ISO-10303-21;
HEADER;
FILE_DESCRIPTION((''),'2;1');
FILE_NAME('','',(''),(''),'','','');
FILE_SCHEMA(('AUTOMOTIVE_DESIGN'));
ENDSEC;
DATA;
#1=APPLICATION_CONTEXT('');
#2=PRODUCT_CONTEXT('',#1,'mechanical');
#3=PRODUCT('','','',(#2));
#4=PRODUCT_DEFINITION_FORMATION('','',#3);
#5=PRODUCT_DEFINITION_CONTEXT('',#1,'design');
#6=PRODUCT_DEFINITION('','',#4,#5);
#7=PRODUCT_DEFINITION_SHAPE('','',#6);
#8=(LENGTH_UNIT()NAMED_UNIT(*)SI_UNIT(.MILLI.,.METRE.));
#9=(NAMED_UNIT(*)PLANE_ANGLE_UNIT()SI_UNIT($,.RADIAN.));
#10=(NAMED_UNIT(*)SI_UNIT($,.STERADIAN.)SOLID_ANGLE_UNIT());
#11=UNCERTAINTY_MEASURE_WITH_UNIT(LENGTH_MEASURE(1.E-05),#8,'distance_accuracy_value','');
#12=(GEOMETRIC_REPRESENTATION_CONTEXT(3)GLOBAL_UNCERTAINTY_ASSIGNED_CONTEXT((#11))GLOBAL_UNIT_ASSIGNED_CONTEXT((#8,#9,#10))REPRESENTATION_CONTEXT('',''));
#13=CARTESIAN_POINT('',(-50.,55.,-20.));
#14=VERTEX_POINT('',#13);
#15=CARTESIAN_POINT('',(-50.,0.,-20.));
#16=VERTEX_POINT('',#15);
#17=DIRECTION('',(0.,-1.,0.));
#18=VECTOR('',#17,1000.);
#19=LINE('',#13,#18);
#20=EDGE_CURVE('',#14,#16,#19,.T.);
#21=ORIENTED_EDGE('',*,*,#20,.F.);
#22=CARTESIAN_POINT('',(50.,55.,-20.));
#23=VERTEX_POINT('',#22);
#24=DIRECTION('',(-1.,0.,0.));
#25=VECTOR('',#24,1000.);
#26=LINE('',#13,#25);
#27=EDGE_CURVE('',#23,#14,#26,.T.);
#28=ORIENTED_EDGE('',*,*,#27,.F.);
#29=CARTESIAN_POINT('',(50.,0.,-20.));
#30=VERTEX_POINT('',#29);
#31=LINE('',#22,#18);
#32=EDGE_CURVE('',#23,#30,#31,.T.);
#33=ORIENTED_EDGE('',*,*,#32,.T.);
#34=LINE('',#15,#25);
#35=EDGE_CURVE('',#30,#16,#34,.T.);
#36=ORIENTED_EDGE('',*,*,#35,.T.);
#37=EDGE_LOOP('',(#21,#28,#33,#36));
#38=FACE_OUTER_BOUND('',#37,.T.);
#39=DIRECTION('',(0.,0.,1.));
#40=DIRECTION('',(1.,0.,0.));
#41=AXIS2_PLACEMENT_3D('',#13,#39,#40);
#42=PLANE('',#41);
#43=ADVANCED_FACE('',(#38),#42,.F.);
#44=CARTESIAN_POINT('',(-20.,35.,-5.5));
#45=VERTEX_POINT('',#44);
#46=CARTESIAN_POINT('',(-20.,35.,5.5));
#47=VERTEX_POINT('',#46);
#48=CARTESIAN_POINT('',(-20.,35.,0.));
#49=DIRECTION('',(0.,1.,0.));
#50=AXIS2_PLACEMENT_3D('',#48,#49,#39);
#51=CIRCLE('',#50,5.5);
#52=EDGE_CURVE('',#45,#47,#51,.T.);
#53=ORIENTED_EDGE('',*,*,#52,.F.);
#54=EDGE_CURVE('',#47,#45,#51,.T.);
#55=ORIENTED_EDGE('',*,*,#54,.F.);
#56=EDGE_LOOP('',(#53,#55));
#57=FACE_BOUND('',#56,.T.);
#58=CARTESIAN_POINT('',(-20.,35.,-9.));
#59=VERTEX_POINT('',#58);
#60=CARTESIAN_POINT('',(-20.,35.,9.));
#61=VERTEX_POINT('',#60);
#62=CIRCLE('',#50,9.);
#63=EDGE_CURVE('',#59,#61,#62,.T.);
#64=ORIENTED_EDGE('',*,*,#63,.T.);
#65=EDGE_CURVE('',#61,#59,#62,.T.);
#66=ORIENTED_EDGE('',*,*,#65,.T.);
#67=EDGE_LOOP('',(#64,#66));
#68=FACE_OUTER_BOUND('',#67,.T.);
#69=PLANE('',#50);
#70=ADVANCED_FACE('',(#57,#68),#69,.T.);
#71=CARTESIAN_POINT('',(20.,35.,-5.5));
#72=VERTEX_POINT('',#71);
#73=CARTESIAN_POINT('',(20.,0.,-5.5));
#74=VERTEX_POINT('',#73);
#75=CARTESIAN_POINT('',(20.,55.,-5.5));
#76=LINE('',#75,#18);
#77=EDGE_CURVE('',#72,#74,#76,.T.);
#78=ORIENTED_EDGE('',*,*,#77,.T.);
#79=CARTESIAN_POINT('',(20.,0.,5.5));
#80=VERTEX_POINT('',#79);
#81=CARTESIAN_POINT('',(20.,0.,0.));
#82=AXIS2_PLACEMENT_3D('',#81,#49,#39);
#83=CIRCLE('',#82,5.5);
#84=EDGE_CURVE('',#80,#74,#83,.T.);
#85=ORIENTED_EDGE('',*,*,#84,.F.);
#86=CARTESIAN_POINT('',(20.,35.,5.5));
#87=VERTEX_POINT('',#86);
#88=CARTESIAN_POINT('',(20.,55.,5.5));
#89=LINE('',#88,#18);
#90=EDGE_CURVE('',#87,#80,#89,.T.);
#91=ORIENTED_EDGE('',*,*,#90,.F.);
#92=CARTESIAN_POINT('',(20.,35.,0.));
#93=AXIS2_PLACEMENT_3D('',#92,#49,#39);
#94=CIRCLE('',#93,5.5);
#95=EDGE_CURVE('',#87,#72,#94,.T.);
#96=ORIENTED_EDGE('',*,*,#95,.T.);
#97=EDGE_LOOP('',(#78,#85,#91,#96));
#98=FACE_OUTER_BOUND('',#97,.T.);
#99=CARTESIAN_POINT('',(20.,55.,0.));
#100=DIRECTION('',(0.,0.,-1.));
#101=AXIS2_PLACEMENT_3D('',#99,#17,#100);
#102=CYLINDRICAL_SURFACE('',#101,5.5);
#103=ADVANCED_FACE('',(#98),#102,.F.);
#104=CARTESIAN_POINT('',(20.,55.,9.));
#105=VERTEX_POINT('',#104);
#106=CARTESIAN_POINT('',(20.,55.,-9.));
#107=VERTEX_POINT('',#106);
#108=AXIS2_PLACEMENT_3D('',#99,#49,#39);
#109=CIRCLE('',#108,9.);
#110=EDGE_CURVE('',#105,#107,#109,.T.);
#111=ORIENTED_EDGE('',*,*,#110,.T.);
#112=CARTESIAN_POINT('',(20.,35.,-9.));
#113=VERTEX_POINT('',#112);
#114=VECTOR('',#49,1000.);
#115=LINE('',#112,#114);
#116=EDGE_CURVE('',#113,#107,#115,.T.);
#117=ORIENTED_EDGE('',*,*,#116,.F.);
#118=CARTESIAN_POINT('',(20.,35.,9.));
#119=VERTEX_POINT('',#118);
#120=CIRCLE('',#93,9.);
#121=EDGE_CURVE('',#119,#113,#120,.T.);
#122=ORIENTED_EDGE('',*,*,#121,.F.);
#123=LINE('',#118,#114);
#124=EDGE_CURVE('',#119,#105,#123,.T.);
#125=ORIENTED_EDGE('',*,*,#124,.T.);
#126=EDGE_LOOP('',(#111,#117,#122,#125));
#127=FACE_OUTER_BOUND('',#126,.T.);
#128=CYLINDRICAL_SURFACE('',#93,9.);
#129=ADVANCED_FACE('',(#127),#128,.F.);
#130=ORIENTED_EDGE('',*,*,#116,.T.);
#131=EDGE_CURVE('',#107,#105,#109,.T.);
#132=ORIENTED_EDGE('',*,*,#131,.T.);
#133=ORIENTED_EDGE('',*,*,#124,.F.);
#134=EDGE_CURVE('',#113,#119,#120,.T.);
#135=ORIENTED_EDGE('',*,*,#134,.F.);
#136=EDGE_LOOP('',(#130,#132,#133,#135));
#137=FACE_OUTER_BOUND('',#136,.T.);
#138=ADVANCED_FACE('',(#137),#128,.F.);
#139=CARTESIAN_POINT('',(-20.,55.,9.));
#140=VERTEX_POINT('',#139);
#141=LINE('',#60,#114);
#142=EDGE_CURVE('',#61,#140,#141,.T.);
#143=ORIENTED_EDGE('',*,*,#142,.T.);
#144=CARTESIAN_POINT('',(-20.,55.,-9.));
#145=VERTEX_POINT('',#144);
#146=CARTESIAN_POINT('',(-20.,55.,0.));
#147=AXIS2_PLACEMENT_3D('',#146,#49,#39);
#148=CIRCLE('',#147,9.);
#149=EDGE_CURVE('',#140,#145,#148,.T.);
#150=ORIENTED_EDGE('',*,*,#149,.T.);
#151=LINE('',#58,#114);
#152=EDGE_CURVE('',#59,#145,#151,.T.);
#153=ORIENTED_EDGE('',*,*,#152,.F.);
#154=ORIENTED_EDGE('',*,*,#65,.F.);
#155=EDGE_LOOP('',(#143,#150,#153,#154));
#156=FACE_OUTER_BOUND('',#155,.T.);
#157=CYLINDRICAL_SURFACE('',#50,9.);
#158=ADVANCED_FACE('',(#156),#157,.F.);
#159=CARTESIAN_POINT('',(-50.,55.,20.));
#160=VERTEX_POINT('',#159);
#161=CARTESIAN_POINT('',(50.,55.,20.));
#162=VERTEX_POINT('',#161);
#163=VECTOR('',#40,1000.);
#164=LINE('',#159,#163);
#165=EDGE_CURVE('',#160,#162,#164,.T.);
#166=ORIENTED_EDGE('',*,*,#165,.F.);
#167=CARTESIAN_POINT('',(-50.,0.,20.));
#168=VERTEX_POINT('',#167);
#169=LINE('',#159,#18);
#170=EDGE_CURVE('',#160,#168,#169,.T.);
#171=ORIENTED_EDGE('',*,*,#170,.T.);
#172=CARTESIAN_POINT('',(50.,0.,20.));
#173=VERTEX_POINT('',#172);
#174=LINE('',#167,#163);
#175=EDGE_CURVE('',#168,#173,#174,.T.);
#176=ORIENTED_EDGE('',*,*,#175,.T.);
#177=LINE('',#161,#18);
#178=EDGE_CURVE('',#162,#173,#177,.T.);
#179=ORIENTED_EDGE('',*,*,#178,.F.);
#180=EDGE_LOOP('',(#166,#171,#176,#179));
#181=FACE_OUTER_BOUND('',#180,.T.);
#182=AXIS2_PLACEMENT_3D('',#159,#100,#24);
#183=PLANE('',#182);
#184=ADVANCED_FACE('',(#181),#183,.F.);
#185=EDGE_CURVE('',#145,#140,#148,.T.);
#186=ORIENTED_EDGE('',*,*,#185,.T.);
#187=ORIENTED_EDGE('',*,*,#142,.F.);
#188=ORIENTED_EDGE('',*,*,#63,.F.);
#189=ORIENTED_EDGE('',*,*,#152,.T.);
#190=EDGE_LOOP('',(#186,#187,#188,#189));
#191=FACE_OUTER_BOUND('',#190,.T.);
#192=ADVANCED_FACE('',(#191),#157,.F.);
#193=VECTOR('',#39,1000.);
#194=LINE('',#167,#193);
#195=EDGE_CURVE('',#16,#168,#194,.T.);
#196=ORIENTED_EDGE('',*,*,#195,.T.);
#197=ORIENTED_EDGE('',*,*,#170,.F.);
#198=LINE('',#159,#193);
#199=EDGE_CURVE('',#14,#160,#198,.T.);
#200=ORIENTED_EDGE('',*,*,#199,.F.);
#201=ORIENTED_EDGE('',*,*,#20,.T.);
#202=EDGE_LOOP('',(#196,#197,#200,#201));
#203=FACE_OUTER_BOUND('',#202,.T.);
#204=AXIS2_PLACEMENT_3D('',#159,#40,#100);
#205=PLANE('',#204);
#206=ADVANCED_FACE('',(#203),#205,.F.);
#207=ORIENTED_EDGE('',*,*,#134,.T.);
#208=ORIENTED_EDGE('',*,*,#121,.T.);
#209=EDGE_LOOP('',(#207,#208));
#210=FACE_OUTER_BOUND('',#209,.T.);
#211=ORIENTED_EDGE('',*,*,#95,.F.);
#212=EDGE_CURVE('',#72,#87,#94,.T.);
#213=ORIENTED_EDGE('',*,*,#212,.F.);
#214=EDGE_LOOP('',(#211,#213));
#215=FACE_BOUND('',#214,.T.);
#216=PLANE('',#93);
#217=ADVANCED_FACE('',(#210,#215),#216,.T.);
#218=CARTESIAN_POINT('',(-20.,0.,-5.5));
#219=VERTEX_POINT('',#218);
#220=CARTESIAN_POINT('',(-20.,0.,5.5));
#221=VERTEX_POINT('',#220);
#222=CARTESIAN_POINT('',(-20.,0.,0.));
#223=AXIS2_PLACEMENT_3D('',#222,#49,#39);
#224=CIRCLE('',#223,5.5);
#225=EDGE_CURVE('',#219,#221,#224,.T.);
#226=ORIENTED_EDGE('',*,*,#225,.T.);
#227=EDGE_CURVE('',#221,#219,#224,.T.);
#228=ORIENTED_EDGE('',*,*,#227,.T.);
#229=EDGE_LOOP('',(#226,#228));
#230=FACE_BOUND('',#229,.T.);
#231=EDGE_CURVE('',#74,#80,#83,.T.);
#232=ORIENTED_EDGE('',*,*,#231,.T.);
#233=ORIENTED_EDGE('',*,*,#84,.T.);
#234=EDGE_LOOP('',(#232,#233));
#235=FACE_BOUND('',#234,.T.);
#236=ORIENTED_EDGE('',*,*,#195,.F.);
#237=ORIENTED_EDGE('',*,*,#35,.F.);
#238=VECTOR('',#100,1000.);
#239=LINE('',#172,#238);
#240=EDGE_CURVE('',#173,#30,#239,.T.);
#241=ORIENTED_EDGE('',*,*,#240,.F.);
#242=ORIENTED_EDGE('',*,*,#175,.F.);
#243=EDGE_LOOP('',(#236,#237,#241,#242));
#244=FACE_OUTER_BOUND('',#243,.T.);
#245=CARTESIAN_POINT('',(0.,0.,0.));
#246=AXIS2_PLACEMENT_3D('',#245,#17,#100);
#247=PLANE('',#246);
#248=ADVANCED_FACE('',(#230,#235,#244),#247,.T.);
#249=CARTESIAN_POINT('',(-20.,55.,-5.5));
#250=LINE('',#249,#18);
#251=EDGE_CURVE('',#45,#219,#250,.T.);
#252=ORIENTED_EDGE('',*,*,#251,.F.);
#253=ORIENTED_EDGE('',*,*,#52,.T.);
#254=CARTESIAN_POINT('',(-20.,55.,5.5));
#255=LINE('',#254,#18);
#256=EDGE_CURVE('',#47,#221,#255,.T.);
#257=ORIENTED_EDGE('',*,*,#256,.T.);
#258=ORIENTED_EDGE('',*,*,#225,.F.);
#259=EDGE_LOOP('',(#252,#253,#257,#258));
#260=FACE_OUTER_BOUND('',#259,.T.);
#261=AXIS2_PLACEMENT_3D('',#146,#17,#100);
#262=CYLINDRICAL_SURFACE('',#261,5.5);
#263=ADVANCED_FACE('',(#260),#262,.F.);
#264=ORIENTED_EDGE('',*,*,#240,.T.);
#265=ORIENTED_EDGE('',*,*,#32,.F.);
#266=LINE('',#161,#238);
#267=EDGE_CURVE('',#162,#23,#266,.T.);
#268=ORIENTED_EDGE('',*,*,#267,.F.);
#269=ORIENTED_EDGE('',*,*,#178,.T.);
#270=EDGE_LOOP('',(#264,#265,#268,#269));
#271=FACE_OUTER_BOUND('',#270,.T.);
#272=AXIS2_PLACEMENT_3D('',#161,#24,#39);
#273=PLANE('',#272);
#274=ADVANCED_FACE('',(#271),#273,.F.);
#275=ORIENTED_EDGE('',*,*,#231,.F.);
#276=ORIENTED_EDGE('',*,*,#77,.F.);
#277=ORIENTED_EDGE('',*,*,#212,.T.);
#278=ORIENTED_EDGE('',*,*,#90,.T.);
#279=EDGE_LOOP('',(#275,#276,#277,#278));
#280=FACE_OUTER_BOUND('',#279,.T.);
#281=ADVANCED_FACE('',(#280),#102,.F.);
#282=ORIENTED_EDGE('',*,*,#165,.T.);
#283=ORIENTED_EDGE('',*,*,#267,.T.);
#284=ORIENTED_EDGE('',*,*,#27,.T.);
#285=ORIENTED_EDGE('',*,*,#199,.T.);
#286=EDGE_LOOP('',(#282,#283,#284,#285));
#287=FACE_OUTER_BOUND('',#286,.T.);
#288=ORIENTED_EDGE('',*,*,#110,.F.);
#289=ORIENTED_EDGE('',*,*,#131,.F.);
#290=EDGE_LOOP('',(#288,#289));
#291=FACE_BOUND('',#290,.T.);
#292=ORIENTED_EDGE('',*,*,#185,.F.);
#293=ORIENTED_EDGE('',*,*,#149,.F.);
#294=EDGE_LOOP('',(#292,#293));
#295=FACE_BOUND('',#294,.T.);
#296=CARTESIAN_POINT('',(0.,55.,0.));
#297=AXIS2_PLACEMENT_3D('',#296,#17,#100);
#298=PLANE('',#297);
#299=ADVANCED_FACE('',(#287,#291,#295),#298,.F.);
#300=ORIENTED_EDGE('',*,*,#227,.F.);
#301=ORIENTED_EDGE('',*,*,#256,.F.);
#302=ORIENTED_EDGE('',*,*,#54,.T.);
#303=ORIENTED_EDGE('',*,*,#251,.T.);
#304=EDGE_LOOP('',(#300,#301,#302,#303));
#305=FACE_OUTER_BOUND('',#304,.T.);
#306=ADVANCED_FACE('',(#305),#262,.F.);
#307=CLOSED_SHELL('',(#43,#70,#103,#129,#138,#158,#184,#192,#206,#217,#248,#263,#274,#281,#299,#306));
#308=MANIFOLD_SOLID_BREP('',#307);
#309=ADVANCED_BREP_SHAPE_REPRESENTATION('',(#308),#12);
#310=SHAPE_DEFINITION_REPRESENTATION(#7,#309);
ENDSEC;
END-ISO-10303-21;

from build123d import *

# Parameters (mm, degrees)
SKETCH1_W           = 100
SKETCH1_H           = 40
SKETCH1_R           = 5.5
BOSS_EXTRUDE1_DEPTH = 55
SKETCH2_R           = 9
CUT_EXTRUDE1_DEPTH  = 20


with BuildPart() as part:
    # Sketch1 → Boss-Extrude1 (new body)
    with BuildSketch(Plane(origin=(0, 0, 0), x_dir=(1, 0, 0), z_dir=(0, 1, 0))):
        Rectangle(SKETCH1_W, SKETCH1_H)
        with Locations(Location((-20, 0, 0), (0, 0, 270))):
            Circle(SKETCH1_R, mode=Mode.SUBTRACT)
        with Locations(Location((20, 0, 0), (0, 0, 270))):
            Circle(SKETCH1_R, mode=Mode.SUBTRACT)
    extrude(amount=BOSS_EXTRUDE1_DEPTH)

    # Sketch2 → Cut-Extrude1 (cut)
    with BuildSketch(Plane(origin=(0, 55, 0), x_dir=(1, 0, 0), z_dir=(0, 1, 0))):
        with Locations(Location((20, 0, 0), (0, 0, 270))):
            Circle(SKETCH2_R)
        with Locations(Location((-20, 0, 0), (0, 0, 270))):
            Circle(SKETCH2_R)
    extrude(amount=-CUT_EXTRUDE1_DEPTH, mode=Mode.SUBTRACT)


solid = part.part
